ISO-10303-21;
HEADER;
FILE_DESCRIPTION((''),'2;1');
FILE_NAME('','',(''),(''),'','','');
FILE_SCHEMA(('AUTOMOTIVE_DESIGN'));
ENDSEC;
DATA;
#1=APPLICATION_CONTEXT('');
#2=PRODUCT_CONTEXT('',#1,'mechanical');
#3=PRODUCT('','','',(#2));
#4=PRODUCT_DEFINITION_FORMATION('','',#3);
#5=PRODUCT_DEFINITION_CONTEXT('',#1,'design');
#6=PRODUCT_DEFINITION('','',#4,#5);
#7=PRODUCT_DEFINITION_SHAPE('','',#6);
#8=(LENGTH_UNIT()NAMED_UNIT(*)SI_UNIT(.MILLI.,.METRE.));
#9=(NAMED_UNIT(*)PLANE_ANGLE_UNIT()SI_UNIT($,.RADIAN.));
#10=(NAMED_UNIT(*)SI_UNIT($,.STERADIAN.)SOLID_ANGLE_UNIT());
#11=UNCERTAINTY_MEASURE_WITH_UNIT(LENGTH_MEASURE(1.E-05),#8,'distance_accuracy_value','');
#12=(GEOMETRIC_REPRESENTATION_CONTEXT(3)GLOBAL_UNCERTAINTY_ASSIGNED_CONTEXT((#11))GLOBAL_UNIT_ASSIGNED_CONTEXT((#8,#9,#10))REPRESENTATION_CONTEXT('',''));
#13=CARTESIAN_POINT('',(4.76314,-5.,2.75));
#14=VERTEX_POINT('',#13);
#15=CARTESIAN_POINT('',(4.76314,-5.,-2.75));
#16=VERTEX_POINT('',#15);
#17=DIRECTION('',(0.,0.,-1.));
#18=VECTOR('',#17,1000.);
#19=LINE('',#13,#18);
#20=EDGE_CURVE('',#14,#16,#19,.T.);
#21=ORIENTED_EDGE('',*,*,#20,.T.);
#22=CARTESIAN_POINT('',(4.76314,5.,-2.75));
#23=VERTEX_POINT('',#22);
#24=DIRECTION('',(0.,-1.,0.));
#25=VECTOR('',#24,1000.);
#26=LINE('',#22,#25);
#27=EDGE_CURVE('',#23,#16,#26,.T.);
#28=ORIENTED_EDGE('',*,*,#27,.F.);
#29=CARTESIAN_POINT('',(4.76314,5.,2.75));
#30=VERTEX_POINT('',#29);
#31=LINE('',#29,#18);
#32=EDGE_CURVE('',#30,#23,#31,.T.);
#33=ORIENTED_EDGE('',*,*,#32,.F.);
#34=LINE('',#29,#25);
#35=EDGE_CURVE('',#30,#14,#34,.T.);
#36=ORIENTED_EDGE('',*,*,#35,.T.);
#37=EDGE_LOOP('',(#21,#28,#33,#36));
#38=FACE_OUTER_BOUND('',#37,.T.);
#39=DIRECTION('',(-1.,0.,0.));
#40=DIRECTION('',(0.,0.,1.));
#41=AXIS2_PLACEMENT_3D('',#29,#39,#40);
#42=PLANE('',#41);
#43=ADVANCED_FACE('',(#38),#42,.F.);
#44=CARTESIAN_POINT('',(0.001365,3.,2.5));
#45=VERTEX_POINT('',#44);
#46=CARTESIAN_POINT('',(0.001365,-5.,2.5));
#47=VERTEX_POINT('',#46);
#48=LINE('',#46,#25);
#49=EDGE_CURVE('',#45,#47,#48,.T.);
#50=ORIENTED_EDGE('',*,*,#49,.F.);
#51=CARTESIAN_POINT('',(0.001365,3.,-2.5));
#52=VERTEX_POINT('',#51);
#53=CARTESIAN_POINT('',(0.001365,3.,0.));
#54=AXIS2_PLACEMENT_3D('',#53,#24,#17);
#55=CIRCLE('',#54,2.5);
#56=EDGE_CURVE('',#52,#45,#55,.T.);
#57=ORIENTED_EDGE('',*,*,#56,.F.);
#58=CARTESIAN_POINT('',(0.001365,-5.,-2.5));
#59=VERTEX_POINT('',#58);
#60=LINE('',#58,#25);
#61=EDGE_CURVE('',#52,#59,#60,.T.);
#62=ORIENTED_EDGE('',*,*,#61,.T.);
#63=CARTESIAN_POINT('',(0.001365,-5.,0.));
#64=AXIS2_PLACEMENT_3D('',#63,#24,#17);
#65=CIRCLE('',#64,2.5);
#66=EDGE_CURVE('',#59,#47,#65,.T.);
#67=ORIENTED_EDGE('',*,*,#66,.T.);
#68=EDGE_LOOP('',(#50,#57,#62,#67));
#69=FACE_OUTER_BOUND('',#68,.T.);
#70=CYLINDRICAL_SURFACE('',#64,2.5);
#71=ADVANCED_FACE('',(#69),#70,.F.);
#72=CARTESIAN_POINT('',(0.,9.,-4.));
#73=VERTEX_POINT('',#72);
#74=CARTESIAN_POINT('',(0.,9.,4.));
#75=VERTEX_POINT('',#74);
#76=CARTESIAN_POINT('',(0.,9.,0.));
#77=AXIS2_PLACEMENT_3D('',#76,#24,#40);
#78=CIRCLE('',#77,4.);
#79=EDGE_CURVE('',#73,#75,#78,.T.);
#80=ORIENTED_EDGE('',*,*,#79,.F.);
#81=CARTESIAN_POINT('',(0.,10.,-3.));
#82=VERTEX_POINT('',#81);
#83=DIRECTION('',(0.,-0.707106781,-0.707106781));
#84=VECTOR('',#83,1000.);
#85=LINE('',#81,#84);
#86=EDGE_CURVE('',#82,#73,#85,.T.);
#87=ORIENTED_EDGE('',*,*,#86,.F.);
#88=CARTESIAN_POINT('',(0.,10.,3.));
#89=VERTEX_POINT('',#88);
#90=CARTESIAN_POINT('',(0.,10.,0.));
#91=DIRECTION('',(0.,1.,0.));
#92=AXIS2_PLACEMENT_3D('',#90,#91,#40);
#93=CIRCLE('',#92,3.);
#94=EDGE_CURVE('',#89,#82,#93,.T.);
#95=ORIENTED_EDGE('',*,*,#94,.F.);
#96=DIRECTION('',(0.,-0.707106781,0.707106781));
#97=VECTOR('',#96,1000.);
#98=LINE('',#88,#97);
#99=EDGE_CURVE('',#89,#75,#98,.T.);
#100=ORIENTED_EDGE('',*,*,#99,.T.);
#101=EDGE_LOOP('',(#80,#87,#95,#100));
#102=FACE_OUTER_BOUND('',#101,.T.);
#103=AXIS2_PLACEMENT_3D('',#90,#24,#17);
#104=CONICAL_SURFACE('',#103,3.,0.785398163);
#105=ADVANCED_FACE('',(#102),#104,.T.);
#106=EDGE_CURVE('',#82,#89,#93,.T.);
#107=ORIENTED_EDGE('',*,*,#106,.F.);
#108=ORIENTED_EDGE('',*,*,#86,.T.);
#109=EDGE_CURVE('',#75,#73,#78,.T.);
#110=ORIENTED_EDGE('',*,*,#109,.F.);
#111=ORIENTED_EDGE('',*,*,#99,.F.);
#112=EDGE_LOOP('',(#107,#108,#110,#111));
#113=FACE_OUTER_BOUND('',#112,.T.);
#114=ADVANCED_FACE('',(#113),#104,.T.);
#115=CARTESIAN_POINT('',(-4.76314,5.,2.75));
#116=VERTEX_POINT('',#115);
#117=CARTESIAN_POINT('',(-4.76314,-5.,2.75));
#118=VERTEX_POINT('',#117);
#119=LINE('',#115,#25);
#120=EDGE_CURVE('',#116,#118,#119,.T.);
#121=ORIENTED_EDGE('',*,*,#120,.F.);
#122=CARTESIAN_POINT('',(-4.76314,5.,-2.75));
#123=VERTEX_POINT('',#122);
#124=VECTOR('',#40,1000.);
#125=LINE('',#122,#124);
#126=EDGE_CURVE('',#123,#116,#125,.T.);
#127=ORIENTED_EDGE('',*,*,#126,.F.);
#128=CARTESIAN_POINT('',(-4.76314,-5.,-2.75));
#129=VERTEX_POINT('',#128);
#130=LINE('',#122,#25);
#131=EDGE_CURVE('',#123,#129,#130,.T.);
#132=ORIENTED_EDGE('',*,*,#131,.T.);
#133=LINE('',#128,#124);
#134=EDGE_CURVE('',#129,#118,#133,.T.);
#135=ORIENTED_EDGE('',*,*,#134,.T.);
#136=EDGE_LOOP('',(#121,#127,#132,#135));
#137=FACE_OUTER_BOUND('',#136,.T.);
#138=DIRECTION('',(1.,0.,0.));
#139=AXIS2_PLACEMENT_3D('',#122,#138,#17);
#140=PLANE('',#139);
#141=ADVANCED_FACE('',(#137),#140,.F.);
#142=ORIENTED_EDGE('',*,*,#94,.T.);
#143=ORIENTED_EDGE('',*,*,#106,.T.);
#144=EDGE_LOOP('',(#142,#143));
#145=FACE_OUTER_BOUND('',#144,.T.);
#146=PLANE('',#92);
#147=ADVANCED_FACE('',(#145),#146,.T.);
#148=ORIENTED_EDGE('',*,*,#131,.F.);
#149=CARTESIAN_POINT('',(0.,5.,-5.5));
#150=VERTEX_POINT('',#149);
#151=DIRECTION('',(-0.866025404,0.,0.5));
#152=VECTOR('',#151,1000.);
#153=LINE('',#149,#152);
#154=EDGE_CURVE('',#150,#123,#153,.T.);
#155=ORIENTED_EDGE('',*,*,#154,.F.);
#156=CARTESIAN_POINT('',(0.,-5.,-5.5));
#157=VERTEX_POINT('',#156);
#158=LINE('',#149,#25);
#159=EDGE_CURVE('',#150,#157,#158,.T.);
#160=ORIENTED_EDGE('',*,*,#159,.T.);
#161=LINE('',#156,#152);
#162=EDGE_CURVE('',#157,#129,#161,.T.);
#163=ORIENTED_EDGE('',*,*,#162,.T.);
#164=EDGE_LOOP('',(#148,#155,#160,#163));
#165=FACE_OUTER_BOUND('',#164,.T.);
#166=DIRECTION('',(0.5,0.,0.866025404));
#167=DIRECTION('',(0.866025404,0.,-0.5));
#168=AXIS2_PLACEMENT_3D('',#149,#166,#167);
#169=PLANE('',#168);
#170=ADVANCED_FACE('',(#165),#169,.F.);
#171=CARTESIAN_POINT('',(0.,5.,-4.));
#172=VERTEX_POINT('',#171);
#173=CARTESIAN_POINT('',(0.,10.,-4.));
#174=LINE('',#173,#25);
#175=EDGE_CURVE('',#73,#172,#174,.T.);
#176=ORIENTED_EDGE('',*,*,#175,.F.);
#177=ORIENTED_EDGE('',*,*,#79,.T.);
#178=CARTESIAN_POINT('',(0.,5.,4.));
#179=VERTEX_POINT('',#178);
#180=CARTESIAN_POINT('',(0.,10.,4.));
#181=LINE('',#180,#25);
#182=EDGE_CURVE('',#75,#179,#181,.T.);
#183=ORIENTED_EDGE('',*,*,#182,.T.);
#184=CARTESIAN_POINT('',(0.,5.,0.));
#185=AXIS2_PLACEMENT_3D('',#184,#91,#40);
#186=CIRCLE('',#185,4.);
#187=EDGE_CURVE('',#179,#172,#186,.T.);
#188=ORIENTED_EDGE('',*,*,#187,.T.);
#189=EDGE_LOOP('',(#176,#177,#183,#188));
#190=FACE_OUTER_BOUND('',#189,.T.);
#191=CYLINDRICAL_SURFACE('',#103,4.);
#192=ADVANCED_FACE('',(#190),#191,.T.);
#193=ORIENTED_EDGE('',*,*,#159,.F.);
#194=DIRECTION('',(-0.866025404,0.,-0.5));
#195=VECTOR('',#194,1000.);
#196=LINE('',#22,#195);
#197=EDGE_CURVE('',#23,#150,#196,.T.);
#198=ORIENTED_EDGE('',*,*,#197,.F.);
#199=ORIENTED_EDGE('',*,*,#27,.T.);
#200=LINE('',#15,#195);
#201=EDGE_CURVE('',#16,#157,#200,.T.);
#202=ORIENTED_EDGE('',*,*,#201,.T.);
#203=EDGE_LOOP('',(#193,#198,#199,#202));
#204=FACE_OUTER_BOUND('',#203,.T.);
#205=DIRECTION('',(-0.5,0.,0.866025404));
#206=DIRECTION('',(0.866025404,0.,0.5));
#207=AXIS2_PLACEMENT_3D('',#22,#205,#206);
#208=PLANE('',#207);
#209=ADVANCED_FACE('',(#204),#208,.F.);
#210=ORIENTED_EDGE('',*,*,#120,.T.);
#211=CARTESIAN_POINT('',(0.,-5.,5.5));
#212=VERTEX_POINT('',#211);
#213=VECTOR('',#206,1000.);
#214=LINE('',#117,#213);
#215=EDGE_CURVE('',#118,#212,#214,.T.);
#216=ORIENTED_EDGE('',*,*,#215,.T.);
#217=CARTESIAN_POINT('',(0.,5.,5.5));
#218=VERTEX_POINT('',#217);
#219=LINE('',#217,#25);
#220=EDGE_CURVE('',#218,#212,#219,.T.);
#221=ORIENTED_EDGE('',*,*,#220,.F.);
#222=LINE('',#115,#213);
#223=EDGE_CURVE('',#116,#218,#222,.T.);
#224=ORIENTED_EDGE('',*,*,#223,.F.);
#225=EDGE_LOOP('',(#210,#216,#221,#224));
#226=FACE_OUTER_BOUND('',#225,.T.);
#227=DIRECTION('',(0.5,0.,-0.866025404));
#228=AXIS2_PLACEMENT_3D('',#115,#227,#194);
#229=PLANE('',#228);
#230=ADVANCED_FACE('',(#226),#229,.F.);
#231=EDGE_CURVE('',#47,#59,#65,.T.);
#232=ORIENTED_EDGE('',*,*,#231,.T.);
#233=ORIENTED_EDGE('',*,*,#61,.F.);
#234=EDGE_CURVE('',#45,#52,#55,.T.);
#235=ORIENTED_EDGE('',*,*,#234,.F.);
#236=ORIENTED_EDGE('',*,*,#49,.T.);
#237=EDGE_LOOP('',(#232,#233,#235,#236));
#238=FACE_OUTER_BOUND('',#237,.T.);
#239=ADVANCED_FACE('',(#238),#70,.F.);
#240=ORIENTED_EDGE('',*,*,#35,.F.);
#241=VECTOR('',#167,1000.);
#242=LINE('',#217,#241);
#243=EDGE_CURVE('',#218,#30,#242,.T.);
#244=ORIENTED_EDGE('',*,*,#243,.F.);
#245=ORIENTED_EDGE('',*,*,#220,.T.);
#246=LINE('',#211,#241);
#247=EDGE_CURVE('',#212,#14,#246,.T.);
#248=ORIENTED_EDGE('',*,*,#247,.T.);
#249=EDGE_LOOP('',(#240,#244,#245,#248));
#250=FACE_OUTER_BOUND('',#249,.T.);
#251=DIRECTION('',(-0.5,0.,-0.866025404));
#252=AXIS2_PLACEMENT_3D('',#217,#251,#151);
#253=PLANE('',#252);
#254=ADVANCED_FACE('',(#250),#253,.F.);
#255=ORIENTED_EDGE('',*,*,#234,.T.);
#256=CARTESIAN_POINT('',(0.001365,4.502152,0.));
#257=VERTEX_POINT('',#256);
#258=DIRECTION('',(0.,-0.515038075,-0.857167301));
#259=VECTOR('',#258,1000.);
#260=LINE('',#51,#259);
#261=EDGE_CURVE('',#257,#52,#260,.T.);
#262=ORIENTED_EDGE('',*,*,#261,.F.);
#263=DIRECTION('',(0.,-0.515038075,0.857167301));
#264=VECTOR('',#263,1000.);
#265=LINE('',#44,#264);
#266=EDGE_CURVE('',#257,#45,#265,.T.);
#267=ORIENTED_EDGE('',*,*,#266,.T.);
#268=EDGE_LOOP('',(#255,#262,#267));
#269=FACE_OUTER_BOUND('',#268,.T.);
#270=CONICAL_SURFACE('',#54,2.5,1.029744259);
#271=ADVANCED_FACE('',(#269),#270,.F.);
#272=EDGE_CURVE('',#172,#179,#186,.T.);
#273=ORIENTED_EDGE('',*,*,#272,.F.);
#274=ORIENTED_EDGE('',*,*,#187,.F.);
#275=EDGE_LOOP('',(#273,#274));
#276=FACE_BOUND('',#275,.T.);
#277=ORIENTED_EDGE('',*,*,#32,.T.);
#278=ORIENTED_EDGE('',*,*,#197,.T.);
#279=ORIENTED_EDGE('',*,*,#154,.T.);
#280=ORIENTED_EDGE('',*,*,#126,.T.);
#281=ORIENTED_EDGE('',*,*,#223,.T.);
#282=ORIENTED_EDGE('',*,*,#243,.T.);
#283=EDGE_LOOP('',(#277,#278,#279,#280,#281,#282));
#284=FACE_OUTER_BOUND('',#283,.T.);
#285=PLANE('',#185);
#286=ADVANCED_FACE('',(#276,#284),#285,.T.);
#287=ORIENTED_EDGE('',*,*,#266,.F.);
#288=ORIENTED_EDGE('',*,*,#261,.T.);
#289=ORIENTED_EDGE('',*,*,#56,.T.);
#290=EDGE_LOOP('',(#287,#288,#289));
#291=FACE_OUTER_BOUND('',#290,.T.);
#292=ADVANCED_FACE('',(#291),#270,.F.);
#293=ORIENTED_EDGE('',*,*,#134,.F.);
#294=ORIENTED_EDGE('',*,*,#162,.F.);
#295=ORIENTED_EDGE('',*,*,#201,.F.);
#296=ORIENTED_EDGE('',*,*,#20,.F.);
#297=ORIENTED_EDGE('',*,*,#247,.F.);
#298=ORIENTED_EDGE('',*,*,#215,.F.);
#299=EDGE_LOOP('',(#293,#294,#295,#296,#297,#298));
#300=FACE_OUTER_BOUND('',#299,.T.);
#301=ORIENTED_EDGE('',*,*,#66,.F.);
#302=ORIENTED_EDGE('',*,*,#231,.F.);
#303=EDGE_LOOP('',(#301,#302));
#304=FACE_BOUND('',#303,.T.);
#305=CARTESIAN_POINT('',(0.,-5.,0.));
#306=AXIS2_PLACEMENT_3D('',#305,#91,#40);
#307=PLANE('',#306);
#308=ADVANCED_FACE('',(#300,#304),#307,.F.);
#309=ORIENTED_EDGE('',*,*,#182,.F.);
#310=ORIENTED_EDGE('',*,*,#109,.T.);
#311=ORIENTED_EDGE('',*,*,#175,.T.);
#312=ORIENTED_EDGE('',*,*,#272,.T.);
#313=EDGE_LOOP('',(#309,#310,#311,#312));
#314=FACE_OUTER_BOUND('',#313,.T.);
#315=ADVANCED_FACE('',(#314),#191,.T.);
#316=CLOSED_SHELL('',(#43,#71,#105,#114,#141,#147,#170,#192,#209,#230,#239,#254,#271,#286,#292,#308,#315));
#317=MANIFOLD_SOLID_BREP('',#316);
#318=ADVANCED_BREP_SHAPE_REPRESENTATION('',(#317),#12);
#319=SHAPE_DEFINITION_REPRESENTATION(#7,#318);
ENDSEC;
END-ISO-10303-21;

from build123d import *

# Parameters (mm, degrees)
BOSS_EXTRUDE1_DEPTH       = 5
SKETCH3_R                 = 4
BOSS_EXTRUDE2_DEPTH       = 5
CHAMFER1_SIZE             = 1
M6X1_0_TAPPED_HOLE1_D     = 5
M6X1_0_TAPPED_HOLE1_DEPTH = 8
M6X1_0_TAPPED_HOLE1_TIP   = 1.502151548


with BuildPart() as part:
    # Sketch1 → Boss-Extrude1 (new, symmetric)
    with BuildSketch(Plane(origin=(0, 0, 0), x_dir=(1, 0, 0), z_dir=(0, 1, 0))):
        Polygon((0, 5.5), (-4.763139721, 2.75), (-4.763139721, -2.75), (0, -5.5), (4.763139721, -2.75), (4.763139721, 2.75), align=None)
    extrude(amount=BOSS_EXTRUDE1_DEPTH, both=True)

    # Sketch3 → Boss-Extrude2 (add)
    with BuildSketch(Plane(origin=(0, 5, 0), x_dir=(1, 0, 0), z_dir=(0, 1, 0))):
        with Locations(Location((0, 0, 0), (0, 0, 270))):
            Circle(SKETCH3_R)
    extrude(amount=BOSS_EXTRUDE2_DEPTH)

    # Chamfer1
    chamfer1_edges = [part.edges().sort_by_distance(p)[0] for p in [
        (0, 10, -4),
    ]]
    chamfer(chamfer1_edges, length=CHAMFER1_SIZE)

    # M6x1.0 Tapped Hole1
    with Locations(Plane(origin=(0, -5, 0), x_dir=(-1, 0, 0), z_dir=(0, -1, 0))):
        with Locations((-0.001364709, 0)):
            Hole(M6X1_0_TAPPED_HOLE1_D / 2, depth=M6X1_0_TAPPED_HOLE1_DEPTH)
            with Locations((0, 0, -(M6X1_0_TAPPED_HOLE1_DEPTH + M6X1_0_TAPPED_HOLE1_TIP / 2))):  # 118° drill point
                Cone(0, M6X1_0_TAPPED_HOLE1_D / 2, M6X1_0_TAPPED_HOLE1_TIP, mode=Mode.SUBTRACT)


solid = part.part
